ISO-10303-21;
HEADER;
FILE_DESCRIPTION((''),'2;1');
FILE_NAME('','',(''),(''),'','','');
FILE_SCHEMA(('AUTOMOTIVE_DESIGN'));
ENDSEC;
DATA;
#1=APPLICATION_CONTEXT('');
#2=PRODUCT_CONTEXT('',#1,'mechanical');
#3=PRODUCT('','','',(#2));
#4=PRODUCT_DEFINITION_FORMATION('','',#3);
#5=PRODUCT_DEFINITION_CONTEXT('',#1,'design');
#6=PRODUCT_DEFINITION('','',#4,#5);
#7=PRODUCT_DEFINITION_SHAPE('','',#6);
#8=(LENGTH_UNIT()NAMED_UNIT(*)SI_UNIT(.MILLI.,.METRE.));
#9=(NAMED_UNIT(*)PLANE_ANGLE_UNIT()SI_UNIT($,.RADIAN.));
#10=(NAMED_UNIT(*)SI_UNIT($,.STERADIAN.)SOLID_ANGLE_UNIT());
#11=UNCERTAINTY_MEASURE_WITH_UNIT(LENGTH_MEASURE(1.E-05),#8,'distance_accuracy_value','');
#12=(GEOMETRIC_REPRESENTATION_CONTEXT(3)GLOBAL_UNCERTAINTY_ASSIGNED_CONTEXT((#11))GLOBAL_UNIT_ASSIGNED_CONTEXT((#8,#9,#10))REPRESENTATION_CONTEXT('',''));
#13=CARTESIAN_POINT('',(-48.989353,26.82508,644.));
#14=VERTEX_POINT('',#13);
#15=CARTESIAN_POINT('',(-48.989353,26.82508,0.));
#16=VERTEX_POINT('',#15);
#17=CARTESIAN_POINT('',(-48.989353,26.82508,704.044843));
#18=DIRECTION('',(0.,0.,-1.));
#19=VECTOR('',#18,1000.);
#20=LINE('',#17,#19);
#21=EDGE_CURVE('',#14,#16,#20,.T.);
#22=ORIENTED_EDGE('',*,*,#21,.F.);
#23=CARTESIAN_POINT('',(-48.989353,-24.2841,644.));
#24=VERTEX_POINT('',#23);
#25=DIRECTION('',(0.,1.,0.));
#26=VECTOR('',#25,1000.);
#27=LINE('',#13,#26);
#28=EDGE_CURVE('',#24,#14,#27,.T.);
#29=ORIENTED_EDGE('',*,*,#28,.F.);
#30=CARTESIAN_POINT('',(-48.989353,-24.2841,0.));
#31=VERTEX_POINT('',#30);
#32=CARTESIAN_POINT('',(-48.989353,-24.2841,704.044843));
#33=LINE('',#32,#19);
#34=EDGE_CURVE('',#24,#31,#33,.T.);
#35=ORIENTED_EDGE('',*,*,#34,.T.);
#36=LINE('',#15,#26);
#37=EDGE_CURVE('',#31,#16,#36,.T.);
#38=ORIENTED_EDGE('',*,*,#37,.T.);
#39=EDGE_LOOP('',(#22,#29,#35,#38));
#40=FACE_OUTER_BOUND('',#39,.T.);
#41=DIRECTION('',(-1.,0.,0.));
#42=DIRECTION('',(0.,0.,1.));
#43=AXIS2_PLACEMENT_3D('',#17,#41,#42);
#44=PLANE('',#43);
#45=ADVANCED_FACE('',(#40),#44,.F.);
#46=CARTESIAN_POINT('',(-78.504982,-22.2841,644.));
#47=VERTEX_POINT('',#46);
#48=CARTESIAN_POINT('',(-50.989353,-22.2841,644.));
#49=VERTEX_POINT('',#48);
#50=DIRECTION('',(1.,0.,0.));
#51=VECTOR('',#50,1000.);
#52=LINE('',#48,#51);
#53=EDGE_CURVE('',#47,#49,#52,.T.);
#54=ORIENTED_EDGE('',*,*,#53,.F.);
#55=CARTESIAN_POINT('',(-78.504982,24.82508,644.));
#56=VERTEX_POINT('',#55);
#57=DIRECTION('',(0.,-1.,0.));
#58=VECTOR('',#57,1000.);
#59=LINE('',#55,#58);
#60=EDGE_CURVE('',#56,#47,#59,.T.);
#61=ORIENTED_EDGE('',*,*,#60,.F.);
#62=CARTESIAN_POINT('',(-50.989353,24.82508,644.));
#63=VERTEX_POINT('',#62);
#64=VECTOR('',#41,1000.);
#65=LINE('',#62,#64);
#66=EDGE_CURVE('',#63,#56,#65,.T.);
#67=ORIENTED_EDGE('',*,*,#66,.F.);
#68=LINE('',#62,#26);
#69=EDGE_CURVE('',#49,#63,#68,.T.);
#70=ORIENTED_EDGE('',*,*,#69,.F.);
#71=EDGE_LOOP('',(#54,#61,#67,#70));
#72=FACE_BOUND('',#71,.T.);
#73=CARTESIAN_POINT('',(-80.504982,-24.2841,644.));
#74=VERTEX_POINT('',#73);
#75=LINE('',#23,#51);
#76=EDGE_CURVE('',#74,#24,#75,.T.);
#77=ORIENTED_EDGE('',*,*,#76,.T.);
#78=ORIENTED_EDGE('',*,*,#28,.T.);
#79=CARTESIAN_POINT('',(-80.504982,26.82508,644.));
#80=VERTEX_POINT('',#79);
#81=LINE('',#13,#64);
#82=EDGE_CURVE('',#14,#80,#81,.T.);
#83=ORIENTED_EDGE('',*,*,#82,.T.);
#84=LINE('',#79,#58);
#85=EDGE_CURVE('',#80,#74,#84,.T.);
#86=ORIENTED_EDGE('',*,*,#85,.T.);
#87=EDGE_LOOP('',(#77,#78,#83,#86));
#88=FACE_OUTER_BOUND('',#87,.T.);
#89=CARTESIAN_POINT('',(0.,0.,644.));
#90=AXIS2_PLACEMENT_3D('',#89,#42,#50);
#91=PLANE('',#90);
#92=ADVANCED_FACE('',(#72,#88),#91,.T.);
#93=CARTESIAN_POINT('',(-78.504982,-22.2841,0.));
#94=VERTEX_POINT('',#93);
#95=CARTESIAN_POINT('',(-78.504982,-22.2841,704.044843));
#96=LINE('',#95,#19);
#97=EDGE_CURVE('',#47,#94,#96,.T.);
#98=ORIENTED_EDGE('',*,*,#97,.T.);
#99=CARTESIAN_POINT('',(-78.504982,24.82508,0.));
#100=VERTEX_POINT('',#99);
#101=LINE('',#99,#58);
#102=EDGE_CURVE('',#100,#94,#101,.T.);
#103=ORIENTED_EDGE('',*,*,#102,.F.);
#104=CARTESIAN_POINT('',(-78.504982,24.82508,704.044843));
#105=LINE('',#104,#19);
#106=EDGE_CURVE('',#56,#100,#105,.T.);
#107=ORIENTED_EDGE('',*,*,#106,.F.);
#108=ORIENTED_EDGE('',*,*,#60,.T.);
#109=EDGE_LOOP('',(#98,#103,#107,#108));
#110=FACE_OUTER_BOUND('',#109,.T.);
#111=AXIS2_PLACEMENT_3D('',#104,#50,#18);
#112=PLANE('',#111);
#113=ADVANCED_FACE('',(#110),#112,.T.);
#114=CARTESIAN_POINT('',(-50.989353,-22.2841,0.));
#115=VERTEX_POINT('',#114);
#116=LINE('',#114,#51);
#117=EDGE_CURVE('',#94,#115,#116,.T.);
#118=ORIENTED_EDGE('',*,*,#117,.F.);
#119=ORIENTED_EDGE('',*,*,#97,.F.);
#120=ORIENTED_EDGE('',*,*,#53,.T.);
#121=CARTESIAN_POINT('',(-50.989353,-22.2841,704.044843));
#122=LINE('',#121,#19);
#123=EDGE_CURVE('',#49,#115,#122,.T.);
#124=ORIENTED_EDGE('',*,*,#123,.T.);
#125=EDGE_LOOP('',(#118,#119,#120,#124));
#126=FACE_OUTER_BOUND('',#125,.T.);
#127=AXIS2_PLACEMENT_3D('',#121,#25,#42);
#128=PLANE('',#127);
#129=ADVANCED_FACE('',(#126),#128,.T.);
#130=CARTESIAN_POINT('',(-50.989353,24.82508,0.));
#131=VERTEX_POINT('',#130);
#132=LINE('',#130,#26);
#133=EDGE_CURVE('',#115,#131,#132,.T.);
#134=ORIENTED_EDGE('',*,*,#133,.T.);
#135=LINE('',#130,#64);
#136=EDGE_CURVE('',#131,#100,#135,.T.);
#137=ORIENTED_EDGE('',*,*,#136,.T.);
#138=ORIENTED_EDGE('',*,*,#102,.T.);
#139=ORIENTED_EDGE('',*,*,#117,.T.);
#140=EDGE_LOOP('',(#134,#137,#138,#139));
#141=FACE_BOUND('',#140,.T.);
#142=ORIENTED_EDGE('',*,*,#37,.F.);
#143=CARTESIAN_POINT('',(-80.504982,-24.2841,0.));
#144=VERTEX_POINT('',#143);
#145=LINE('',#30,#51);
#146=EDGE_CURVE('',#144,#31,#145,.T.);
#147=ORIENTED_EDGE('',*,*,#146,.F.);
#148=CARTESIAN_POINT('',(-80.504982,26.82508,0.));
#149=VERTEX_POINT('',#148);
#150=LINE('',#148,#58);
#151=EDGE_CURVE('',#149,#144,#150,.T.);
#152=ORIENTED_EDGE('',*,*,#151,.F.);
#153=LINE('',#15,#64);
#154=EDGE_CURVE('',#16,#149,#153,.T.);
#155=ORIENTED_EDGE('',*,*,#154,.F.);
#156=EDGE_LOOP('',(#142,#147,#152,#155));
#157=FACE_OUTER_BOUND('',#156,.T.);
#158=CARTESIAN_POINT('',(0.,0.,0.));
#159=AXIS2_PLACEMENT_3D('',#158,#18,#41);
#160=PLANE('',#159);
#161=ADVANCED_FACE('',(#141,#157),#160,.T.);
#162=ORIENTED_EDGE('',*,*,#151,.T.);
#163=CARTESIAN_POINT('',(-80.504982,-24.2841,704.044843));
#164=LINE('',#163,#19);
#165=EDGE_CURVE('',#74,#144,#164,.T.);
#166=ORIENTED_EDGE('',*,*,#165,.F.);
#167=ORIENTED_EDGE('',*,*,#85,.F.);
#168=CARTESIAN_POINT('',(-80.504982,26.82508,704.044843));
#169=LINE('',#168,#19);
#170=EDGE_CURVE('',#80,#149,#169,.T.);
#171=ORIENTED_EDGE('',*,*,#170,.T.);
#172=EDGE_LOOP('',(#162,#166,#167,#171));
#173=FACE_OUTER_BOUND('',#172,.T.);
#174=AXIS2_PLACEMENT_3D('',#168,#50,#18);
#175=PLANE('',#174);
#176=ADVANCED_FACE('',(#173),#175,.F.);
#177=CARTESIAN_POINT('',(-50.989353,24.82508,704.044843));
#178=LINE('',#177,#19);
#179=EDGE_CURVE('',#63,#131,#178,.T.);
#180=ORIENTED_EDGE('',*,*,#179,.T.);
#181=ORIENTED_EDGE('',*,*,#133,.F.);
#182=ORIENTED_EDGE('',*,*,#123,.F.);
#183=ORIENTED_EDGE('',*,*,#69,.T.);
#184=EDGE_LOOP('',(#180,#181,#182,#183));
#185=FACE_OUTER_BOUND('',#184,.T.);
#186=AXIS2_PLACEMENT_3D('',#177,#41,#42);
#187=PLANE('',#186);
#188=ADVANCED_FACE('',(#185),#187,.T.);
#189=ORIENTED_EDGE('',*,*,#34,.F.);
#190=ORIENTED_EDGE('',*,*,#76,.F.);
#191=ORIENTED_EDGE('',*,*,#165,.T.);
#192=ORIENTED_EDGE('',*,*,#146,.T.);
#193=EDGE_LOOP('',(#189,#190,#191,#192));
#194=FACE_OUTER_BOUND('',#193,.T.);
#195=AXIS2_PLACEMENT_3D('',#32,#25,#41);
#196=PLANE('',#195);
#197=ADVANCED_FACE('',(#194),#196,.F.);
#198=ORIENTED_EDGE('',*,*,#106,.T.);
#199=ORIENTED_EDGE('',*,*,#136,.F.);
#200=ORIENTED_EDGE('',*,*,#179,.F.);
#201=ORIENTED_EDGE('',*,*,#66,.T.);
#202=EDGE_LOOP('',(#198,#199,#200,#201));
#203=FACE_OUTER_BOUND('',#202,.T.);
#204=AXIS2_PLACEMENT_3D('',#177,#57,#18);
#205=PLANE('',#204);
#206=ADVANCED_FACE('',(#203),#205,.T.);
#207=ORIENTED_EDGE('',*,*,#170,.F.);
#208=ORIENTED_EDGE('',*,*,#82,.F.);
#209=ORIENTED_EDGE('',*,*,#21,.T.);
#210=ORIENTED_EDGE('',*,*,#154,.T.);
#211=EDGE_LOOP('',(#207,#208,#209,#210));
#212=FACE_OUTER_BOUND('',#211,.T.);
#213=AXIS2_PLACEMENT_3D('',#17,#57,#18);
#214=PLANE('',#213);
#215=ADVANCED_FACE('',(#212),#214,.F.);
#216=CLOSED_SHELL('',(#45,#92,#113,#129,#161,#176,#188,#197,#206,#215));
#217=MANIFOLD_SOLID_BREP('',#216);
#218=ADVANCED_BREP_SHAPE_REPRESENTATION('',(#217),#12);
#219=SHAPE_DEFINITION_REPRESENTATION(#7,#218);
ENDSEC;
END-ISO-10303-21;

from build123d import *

# Parameters (mm, degrees)
SKETCH1_W           = 31.515629069
SKETCH1_H           = 51.109180057
SKETCH1_W_2         = 27.515629069
SKETCH1_H_2         = 47.109180057
BOSS_EXTRUDE1_DEPTH = 644


with BuildPart() as part:
    # Sketch1 → Boss-Extrude1 (new body)
    with BuildSketch(Plane.XY):
        with Locations((-64.747167395, 1.270489558)):
            Rectangle(SKETCH1_W, SKETCH1_H)
        with Locations((-64.747167395, 1.270489558)):
            Rectangle(SKETCH1_W_2, SKETCH1_H_2, mode=Mode.SUBTRACT)
    extrude(amount=BOSS_EXTRUDE1_DEPTH)


solid = part.part
